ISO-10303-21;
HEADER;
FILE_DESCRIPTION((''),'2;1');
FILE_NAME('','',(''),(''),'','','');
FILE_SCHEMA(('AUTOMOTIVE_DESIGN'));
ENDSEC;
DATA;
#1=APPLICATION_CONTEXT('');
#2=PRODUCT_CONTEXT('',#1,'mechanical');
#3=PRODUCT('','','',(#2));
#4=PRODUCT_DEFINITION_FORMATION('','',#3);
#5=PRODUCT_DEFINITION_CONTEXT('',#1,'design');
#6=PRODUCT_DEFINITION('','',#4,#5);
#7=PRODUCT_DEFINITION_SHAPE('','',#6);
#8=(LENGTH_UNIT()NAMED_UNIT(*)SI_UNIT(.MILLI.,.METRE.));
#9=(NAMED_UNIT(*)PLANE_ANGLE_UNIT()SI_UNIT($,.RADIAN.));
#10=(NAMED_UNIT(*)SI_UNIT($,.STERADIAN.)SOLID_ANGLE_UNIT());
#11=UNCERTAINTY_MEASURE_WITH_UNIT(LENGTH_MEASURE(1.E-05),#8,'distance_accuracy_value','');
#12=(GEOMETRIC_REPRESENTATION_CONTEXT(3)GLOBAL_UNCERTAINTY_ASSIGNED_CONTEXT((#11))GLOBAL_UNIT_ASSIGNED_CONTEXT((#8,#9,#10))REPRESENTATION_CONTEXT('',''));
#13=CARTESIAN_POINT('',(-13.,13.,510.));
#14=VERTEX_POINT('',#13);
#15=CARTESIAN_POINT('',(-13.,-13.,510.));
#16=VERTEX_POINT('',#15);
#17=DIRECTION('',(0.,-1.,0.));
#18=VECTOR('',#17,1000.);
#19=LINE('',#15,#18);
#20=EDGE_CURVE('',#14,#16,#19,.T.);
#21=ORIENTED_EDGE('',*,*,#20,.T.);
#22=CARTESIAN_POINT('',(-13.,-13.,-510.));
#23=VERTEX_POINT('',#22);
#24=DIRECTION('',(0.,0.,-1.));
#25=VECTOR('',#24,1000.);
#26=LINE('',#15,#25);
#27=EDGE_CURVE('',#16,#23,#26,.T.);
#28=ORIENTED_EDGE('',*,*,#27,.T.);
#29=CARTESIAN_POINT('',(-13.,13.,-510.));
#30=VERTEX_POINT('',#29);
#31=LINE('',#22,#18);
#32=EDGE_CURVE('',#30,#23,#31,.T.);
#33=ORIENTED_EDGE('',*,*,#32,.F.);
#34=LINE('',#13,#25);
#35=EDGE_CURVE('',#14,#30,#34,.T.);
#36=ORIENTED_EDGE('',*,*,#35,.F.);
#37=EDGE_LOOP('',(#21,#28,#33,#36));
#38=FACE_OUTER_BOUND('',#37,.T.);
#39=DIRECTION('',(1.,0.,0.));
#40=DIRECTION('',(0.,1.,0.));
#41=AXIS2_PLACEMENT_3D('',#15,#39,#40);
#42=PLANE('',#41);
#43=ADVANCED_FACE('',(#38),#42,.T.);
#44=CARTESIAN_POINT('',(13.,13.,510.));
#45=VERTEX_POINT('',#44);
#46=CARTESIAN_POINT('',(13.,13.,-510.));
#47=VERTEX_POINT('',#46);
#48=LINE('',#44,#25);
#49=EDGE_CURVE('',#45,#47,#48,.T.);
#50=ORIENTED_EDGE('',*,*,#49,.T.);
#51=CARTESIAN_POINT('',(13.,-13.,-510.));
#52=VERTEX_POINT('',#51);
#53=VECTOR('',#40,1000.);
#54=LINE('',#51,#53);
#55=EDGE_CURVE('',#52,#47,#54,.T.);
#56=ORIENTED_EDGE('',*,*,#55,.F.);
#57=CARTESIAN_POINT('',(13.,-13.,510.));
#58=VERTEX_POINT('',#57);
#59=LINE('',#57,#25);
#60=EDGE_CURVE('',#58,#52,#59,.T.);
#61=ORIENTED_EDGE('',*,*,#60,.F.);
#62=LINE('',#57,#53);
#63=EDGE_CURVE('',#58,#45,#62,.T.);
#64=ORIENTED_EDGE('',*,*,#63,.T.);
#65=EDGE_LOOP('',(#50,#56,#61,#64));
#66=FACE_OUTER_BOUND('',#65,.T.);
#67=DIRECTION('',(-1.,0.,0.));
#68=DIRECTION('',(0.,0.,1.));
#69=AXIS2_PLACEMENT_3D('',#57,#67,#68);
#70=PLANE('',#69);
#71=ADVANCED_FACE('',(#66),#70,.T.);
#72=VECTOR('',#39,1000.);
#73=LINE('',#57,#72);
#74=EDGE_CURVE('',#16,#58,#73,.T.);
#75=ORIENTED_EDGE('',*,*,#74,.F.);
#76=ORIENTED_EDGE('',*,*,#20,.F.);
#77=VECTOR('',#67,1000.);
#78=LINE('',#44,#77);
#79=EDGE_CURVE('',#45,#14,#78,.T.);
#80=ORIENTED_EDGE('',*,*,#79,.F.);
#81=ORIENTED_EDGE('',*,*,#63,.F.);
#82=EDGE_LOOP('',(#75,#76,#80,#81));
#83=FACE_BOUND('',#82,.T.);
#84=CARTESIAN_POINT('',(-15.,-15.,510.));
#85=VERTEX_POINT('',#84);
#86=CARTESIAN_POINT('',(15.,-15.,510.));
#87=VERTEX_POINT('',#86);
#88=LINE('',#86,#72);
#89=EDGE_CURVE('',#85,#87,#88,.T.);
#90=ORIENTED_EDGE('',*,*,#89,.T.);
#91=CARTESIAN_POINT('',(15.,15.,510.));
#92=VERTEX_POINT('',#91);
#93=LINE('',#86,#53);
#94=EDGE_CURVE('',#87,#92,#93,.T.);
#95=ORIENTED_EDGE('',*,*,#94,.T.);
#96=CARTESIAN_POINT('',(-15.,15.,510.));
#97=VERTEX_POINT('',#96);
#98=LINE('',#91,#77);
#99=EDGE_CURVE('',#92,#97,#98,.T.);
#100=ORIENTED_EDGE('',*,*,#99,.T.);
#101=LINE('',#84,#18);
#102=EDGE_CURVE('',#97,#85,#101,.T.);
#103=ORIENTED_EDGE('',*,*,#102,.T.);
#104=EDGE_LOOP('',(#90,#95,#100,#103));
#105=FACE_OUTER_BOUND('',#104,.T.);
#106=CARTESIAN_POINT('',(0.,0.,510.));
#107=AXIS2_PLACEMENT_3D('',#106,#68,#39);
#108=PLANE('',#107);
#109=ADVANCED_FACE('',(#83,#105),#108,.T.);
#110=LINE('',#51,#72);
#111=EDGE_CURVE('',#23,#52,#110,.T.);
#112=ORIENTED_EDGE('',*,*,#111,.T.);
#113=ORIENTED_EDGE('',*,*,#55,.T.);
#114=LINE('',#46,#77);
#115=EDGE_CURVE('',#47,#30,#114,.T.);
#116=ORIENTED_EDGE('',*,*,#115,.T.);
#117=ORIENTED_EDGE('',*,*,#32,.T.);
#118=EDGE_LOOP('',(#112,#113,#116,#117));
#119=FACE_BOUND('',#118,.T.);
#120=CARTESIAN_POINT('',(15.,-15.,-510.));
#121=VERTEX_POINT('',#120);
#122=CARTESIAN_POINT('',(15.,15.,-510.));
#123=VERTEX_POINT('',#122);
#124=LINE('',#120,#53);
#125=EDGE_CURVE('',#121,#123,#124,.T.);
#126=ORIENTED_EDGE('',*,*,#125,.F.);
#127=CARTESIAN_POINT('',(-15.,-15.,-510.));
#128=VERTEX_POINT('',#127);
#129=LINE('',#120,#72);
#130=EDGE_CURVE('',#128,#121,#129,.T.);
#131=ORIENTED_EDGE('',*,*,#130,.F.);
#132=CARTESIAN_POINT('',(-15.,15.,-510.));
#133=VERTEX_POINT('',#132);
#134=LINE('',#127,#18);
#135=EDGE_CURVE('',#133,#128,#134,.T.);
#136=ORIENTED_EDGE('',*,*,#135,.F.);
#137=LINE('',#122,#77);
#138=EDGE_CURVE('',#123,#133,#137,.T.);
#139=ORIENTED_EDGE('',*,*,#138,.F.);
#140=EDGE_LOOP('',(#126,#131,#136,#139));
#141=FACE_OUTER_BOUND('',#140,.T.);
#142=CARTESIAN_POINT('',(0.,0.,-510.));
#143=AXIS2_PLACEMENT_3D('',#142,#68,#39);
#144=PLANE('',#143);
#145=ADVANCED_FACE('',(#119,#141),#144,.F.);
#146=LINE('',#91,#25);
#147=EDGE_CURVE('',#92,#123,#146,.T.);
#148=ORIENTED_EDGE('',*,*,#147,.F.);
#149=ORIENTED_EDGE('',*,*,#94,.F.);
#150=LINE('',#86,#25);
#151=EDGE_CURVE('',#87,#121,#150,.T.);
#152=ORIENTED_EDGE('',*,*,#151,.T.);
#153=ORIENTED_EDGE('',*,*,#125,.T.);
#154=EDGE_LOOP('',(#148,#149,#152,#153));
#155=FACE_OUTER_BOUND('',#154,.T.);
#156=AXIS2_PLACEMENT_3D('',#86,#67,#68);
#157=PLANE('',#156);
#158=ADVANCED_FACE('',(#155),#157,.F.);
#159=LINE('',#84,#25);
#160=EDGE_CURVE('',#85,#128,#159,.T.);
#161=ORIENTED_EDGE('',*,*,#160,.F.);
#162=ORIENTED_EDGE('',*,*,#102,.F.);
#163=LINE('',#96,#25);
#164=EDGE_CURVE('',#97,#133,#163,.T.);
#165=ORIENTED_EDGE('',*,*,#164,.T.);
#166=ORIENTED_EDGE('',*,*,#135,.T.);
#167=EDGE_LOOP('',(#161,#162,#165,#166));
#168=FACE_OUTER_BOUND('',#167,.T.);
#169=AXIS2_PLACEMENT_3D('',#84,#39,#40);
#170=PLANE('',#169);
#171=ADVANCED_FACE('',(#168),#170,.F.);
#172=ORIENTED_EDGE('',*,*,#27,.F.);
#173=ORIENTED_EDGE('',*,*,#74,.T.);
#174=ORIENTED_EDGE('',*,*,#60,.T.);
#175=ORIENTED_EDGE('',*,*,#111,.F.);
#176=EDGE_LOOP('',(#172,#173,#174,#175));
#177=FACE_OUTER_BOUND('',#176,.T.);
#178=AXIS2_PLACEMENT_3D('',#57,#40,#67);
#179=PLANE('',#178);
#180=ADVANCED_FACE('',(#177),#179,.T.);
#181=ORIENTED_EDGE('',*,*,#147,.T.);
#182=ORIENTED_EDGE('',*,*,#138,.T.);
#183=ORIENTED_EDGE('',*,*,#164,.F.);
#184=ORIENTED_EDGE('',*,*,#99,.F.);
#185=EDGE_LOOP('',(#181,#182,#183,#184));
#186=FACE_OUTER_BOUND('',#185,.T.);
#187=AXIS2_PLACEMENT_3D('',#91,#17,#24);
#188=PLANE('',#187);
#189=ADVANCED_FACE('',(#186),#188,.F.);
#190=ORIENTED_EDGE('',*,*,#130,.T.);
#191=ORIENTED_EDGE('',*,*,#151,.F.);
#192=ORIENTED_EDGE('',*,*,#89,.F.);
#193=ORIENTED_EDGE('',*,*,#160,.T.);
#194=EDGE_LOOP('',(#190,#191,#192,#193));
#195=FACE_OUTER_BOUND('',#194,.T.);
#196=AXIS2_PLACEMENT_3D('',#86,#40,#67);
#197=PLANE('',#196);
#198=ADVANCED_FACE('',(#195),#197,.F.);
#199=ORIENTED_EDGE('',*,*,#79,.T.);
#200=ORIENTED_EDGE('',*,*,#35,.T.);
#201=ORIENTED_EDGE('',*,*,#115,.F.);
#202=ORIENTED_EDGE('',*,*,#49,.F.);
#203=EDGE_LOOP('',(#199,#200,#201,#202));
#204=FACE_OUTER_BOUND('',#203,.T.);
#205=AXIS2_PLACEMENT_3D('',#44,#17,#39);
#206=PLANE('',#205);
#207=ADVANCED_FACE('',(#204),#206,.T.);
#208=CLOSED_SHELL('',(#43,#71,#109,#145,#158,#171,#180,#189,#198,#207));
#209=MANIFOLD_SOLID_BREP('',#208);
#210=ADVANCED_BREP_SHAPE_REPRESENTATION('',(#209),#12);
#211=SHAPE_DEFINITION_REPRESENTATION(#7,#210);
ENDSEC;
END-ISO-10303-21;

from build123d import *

# Parameters (mm, degrees)
SKETCH_1_W      = 30
SKETCH_1_H      = 30
SKETCH_1_W_2    = 26
SKETCH_1_H_2    = 26
EXTRUDE_1_DEPTH = 510


with BuildPart() as part:
    # 草图1 → 凸台-拉伸1 (new, symmetric)
    with BuildSketch(Plane.XY):
        Rectangle(SKETCH_1_W, SKETCH_1_H)
        Rectangle(SKETCH_1_W_2, SKETCH_1_H_2, mode=Mode.SUBTRACT)
    extrude(amount=EXTRUDE_1_DEPTH, both=True)


solid = part.part
